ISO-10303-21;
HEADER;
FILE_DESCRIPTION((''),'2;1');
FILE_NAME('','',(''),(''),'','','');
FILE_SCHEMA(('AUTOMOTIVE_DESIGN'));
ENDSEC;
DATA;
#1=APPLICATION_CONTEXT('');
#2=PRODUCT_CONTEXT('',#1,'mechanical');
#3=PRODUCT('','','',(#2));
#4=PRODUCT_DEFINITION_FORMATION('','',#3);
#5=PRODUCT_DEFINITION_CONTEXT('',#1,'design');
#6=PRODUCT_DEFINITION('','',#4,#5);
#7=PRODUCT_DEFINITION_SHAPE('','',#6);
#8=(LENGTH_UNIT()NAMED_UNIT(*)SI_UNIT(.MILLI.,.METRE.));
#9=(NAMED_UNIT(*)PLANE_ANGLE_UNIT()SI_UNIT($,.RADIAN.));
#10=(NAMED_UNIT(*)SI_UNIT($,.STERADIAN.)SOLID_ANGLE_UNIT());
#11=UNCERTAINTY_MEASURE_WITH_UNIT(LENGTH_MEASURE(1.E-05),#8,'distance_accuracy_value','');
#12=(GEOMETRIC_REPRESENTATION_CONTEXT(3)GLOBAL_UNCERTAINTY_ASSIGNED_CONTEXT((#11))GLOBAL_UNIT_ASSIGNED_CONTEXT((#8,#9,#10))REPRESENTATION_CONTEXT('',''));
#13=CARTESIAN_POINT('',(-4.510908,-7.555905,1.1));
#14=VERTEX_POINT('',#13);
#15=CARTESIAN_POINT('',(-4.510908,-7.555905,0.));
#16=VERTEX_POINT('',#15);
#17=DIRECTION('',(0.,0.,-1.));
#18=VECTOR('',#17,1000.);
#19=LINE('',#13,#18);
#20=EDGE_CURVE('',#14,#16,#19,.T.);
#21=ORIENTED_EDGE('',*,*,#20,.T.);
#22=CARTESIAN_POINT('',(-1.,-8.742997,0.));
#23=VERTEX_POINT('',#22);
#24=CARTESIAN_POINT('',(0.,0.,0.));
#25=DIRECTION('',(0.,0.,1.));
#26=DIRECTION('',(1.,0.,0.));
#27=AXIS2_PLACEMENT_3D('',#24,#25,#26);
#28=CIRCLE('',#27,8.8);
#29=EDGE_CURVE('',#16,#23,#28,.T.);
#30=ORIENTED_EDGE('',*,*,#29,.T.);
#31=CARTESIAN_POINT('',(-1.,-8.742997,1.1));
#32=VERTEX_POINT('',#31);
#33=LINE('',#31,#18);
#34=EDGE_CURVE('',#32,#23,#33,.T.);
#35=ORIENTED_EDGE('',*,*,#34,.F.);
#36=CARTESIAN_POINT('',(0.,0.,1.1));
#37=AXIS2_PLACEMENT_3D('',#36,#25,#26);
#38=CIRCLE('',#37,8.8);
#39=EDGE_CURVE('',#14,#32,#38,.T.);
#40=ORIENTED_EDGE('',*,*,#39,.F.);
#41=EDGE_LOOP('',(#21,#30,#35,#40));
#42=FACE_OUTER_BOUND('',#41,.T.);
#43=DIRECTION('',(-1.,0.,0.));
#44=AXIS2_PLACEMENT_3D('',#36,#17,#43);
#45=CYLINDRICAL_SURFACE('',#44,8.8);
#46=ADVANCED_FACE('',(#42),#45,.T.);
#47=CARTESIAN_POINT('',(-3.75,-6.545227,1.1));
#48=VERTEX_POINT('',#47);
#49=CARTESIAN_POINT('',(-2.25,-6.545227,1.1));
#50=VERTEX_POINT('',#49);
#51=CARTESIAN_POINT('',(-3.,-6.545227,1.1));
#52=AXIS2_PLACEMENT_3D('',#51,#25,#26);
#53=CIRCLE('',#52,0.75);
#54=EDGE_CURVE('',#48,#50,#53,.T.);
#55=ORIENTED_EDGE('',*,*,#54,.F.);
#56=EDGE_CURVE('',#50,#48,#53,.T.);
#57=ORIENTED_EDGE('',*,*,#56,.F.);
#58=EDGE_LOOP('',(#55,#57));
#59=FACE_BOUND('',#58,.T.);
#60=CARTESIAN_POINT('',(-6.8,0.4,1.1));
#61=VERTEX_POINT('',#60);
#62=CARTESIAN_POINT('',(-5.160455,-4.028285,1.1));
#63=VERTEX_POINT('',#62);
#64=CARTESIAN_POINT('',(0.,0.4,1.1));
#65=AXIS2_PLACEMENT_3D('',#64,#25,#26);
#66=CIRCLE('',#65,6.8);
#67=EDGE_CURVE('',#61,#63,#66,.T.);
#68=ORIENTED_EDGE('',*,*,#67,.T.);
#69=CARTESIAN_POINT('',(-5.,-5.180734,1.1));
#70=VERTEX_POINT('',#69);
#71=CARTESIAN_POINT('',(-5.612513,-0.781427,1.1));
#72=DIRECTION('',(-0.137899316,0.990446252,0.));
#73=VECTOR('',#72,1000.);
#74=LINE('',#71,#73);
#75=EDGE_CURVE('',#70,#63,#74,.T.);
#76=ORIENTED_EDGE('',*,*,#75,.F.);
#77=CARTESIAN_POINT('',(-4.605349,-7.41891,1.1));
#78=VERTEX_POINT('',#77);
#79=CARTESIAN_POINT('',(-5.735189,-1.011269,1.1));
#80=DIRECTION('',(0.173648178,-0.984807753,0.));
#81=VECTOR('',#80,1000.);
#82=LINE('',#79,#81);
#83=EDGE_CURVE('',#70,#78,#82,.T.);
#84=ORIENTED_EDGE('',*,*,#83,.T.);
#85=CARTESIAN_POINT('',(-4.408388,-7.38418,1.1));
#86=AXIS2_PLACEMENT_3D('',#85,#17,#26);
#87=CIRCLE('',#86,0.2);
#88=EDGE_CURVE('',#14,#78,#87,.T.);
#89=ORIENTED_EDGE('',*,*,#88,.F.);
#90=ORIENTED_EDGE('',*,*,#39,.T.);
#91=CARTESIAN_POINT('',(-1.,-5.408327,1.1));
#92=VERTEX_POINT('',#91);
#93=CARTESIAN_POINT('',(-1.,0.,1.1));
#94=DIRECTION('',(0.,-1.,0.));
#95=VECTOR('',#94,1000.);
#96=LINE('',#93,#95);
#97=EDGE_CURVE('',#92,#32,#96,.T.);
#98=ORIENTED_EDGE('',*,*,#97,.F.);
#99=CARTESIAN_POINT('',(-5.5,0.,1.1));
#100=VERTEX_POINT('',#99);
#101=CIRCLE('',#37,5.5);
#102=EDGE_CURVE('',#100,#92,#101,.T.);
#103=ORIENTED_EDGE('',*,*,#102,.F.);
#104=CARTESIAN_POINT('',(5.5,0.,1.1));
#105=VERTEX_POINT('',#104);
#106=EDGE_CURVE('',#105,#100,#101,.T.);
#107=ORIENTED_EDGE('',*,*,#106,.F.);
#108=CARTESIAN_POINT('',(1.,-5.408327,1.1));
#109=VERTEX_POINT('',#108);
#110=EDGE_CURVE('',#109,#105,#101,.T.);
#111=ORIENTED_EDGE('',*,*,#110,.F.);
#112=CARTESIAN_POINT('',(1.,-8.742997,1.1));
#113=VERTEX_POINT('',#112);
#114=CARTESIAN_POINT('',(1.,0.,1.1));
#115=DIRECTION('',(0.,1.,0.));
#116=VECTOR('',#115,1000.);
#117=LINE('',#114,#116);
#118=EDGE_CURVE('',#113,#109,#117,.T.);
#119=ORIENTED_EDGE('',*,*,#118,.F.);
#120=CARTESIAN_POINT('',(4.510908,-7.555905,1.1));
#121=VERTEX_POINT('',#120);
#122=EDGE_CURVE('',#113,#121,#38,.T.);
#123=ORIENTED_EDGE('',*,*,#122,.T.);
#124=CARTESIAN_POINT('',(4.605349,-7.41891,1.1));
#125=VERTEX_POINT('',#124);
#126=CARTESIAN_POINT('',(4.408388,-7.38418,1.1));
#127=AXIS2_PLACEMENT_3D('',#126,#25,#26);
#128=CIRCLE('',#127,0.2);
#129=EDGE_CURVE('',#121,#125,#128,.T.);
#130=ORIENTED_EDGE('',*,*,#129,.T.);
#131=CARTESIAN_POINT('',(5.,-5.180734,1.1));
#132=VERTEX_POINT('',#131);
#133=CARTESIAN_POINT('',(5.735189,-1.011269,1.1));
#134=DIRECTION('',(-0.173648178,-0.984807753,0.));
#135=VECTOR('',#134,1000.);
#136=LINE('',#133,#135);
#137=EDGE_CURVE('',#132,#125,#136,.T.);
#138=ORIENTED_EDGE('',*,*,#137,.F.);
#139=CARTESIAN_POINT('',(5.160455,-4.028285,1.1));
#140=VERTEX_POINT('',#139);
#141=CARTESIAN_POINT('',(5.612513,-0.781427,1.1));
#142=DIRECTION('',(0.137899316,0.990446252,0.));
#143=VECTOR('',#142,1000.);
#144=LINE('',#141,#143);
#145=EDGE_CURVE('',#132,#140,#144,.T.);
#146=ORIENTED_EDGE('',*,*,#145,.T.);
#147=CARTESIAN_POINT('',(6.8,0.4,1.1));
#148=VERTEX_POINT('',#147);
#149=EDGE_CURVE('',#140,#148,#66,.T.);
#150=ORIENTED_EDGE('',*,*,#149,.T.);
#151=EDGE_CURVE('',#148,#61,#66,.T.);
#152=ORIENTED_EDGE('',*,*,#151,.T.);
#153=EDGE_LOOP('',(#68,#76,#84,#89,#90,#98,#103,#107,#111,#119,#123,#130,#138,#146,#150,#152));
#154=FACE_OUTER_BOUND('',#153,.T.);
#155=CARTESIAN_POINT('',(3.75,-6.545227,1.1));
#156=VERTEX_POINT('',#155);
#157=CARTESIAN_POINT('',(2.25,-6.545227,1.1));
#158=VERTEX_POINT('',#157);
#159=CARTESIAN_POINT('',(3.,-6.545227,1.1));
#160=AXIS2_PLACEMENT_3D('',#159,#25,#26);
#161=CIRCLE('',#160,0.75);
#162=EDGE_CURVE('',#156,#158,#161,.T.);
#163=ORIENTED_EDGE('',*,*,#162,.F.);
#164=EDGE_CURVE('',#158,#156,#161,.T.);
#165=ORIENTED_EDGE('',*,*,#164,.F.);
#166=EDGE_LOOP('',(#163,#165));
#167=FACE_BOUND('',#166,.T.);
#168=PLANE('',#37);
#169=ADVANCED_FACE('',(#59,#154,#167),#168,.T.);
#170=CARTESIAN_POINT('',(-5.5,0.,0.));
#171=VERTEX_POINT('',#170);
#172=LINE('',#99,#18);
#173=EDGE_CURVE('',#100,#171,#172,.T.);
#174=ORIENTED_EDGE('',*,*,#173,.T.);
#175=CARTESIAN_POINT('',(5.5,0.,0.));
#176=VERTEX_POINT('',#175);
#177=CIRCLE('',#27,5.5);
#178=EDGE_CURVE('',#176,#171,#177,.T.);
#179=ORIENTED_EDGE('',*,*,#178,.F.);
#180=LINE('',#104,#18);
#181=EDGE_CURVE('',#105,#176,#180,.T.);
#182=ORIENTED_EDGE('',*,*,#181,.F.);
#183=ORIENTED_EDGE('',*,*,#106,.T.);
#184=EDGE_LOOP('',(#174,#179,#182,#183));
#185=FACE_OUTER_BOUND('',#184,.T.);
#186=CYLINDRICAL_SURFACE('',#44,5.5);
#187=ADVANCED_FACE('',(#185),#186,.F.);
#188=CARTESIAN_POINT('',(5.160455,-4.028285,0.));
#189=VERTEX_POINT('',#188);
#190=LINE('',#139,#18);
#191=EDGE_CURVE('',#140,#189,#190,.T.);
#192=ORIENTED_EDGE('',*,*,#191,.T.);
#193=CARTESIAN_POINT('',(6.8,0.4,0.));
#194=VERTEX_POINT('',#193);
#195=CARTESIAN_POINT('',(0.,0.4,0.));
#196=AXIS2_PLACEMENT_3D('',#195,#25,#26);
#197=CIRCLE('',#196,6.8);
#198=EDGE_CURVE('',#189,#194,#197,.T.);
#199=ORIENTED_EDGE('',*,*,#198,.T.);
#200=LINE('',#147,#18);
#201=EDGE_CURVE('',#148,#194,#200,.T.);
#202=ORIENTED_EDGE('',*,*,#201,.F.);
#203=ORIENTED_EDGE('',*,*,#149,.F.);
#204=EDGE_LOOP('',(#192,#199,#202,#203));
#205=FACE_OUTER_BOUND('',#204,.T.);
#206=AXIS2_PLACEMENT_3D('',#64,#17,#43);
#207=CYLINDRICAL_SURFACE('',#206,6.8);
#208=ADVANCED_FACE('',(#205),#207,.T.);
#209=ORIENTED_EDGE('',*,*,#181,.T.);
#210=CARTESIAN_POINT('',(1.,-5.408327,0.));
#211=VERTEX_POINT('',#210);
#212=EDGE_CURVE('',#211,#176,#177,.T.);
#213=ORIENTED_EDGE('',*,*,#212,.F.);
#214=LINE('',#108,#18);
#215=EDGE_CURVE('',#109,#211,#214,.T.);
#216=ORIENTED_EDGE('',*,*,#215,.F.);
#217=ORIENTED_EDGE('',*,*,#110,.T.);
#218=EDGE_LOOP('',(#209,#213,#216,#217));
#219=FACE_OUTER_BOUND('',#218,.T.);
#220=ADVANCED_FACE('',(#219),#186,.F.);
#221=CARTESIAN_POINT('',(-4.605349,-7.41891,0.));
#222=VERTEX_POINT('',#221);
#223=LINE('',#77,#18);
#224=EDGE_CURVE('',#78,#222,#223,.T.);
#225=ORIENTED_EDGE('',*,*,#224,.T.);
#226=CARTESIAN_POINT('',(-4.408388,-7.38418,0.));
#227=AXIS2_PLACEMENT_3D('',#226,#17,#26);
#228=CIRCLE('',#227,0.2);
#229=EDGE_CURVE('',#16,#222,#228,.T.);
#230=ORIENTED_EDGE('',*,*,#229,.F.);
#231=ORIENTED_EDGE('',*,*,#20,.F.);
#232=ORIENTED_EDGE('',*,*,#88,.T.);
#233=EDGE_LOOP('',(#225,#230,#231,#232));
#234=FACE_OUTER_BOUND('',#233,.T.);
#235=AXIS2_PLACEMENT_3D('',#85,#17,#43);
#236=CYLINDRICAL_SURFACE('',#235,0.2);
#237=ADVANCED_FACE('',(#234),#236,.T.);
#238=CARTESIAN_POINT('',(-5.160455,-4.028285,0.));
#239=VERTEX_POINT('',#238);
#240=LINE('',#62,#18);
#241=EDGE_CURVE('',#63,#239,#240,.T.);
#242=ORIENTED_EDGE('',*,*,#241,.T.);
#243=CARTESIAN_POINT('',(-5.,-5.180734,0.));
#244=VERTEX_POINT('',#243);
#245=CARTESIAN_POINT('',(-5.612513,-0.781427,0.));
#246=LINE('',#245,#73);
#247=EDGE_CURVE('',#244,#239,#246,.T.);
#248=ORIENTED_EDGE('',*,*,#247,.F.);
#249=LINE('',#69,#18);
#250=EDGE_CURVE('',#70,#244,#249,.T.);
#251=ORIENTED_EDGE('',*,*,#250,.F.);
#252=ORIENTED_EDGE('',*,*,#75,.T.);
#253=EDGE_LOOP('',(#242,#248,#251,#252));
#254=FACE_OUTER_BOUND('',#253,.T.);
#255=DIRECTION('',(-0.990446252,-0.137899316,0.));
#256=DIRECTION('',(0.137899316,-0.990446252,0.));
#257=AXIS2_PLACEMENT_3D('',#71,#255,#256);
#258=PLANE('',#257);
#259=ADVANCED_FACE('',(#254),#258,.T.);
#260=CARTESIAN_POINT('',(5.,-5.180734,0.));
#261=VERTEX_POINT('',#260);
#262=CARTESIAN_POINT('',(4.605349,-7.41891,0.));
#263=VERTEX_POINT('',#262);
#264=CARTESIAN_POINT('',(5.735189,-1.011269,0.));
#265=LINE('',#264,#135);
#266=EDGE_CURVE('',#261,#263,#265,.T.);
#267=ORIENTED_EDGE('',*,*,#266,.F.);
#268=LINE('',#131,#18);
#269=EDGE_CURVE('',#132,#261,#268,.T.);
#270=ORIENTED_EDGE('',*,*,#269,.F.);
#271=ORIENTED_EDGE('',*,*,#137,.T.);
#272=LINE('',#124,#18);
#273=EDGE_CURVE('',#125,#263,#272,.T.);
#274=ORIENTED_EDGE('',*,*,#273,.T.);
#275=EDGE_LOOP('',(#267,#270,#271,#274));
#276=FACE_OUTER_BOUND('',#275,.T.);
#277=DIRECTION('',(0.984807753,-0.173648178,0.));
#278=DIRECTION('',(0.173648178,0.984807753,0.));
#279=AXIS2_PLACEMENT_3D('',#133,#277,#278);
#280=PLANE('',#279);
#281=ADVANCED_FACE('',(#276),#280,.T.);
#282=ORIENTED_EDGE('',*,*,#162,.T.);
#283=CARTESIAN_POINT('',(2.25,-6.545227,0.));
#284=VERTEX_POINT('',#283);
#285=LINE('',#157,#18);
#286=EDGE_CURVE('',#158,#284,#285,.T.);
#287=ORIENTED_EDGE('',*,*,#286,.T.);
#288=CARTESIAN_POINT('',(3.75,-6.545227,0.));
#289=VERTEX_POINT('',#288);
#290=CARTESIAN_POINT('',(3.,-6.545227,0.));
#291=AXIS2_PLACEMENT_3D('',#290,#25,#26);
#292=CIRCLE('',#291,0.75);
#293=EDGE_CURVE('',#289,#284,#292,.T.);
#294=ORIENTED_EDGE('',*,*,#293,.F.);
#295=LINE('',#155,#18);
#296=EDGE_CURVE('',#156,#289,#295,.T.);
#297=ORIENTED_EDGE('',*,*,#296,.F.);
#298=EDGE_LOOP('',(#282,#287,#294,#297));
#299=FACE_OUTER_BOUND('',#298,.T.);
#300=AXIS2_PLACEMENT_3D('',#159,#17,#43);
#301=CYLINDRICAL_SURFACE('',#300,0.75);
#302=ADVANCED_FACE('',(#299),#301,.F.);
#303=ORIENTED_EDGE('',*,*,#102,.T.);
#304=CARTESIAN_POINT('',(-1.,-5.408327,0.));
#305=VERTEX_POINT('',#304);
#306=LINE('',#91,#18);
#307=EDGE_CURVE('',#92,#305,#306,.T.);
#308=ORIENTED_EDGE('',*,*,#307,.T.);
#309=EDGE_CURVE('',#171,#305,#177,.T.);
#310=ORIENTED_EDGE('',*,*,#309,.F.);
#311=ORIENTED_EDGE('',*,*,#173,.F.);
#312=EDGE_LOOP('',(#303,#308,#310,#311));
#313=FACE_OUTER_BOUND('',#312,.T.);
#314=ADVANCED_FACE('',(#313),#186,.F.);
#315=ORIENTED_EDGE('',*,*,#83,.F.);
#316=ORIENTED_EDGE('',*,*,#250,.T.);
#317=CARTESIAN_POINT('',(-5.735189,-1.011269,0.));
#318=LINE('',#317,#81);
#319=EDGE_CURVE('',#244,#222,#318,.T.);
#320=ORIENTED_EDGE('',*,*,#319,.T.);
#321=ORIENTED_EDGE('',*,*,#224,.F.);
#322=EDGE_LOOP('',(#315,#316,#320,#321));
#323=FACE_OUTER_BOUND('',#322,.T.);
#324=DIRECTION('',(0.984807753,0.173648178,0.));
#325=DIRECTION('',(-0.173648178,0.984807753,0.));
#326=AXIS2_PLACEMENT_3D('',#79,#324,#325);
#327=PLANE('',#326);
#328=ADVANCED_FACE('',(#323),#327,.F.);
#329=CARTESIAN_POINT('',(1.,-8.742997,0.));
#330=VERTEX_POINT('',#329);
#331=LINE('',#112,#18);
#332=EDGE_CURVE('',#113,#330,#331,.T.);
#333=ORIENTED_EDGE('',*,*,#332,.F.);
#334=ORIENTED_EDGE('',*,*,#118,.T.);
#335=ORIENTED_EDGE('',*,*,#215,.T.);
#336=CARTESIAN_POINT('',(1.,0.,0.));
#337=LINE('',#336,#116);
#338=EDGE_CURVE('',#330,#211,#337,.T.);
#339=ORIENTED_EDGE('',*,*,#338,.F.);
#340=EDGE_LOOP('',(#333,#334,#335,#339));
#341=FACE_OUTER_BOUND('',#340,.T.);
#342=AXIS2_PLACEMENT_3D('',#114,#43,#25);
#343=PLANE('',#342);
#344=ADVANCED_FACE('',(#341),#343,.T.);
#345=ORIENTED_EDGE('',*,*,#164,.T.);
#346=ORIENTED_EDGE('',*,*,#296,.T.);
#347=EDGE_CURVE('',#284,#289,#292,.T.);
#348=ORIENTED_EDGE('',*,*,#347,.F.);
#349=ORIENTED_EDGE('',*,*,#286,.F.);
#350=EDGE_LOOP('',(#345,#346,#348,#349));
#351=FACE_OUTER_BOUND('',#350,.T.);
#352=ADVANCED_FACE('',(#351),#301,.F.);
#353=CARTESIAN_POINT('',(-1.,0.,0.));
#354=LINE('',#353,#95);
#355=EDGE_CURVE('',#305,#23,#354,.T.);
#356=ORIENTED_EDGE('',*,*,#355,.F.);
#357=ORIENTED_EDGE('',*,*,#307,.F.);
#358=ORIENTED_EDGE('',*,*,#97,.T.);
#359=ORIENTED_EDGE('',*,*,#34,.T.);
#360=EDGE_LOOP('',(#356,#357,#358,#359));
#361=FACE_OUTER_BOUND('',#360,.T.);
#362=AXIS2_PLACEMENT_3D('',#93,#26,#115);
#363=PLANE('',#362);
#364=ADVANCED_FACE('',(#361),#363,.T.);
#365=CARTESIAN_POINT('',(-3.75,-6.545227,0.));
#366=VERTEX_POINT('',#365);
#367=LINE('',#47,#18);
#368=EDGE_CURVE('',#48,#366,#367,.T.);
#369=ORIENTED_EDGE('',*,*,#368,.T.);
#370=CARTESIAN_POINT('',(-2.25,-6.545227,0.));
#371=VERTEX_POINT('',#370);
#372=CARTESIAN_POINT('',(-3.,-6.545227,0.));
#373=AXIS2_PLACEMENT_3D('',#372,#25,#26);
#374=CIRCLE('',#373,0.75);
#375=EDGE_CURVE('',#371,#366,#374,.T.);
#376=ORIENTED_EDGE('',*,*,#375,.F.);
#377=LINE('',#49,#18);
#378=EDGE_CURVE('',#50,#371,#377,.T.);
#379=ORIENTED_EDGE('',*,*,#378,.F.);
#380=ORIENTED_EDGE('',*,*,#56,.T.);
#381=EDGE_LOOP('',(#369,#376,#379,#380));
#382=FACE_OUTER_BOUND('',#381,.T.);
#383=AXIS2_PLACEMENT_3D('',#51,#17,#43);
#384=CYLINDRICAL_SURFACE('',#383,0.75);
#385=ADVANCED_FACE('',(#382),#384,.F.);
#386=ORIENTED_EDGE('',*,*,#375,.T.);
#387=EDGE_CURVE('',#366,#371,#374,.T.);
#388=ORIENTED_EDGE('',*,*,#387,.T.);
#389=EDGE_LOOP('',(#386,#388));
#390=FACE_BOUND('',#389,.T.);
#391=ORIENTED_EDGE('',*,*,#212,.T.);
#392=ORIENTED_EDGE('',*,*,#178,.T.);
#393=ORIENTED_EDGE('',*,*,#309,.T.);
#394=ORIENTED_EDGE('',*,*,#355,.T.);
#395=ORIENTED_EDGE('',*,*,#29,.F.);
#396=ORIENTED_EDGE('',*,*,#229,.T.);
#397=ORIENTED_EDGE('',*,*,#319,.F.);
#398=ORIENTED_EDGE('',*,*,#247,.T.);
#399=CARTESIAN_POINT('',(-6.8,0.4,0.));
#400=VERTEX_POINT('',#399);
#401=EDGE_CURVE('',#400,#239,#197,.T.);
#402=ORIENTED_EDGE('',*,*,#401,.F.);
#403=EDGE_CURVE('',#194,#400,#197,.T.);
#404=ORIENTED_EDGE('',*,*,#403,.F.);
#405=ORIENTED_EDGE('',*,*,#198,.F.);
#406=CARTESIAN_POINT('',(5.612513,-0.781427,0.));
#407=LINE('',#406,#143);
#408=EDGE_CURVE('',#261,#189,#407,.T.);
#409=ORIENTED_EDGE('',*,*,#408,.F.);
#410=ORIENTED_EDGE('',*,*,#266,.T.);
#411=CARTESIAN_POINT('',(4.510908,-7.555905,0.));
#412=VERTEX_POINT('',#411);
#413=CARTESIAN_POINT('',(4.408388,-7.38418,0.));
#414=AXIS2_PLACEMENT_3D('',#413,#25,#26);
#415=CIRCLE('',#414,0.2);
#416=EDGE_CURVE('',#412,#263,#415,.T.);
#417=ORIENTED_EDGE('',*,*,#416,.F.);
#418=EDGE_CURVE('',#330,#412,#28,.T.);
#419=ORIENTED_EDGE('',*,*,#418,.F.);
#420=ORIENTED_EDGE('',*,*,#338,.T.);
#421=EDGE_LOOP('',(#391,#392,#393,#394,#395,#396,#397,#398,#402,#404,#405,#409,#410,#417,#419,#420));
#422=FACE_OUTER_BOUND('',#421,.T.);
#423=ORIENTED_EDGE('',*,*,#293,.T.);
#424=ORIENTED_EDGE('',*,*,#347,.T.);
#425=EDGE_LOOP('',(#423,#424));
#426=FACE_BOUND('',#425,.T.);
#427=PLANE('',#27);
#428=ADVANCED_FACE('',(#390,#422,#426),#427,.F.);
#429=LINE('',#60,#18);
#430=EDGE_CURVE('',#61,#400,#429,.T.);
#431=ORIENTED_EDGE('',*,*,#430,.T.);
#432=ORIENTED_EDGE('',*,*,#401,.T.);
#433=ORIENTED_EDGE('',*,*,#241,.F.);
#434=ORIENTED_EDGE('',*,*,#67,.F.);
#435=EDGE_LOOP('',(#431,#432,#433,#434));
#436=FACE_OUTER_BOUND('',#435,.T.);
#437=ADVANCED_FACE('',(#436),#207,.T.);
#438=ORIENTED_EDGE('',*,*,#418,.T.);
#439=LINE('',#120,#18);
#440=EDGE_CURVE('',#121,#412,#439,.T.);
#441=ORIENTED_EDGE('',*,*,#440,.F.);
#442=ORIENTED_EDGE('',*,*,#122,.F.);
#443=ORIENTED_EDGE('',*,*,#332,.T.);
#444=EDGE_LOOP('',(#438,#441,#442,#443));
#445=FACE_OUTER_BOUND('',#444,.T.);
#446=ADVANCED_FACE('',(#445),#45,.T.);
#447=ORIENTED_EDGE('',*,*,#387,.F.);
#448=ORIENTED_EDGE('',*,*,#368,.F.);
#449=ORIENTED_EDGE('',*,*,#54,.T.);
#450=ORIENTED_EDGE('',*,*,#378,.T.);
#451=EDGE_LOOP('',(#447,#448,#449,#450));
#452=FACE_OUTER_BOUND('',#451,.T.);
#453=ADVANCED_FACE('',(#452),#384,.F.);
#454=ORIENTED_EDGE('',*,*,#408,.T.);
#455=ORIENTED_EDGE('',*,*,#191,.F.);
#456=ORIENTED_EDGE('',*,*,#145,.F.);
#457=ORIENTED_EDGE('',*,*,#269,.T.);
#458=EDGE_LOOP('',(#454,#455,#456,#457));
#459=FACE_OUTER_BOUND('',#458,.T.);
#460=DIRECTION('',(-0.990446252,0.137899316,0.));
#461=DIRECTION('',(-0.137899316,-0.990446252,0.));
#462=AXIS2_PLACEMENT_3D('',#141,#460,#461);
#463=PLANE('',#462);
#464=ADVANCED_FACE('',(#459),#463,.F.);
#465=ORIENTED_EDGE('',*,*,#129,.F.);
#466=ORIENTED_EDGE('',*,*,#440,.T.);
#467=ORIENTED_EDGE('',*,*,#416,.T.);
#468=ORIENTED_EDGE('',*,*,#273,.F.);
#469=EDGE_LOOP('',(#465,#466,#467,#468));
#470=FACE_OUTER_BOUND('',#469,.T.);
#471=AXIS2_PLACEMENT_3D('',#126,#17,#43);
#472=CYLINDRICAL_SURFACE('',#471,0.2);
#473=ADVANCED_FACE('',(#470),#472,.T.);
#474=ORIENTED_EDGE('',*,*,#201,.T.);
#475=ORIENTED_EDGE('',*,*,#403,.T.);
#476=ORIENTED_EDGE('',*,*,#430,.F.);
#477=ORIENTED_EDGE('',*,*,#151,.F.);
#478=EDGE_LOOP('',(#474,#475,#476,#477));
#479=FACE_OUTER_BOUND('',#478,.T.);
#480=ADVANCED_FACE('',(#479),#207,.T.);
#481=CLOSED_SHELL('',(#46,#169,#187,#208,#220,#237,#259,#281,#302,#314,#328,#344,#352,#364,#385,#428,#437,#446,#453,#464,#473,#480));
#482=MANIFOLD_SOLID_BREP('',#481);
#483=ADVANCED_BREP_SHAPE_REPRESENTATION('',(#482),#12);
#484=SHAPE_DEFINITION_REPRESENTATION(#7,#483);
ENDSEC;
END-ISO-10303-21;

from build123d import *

# Parameters (mm, degrees)
SKETCH1_R           = 0.75
BOSS_EXTRUDE1_DEPTH = 1.1


with BuildPart() as part:
    # Sketch1 → Boss-Extrude1 (new body)
    with BuildSketch(Plane.XY):
        with BuildLine():
            Line((1, -5.408326913), (1, -6.326068688))
            Line((1, -6.326068688), (1, -7.130217388))
            Line((1, -7.130217388), (1, -8.742997198))
            ThreePointArc((1, -8.742997198), (2.818656417, -8.336376671), (4.510908199, -7.555905454))
            ThreePointArc((4.510908199, -7.555905454), (4.573051873, -7.497695365), (4.605349108, -7.418909965))
            Line((4.605349108, -7.418909965), (5, -5.180733539))
            Line((5, -5.180733539), (5.160454845, -4.028284746))
            ThreePointArc((5.160454845, -4.028284746), (0, 7.2), (-5.160454845, -4.028284746))
            Line((-5.160454845, -4.028284746), (-5, -5.180733539))
            Line((-5, -5.180733539), (-4.605349108, -7.418909965))
            ThreePointArc((-4.605349108, -7.418909965), (-4.573051873, -7.497695365), (-4.510908199, -7.555905454))
            ThreePointArc((-4.510908199, -7.555905454), (-2.818656417, -8.336376671), (-1, -8.742997198))
            Line((-1, -8.742997198), (-1, -7.130217388))
            Line((-1, -7.130217388), (-1, -5.408326913))
            ThreePointArc((-1, -5.408326913), (0, 5.5), (1, -5.408326913))
        make_face()
        with Locations((-3, -6.545227269)):
            Circle(SKETCH1_R, mode=Mode.SUBTRACT)
        with Locations((3, -6.545227269)):
            Circle(SKETCH1_R, mode=Mode.SUBTRACT)
    extrude(amount=BOSS_EXTRUDE1_DEPTH)


solid = part.part
